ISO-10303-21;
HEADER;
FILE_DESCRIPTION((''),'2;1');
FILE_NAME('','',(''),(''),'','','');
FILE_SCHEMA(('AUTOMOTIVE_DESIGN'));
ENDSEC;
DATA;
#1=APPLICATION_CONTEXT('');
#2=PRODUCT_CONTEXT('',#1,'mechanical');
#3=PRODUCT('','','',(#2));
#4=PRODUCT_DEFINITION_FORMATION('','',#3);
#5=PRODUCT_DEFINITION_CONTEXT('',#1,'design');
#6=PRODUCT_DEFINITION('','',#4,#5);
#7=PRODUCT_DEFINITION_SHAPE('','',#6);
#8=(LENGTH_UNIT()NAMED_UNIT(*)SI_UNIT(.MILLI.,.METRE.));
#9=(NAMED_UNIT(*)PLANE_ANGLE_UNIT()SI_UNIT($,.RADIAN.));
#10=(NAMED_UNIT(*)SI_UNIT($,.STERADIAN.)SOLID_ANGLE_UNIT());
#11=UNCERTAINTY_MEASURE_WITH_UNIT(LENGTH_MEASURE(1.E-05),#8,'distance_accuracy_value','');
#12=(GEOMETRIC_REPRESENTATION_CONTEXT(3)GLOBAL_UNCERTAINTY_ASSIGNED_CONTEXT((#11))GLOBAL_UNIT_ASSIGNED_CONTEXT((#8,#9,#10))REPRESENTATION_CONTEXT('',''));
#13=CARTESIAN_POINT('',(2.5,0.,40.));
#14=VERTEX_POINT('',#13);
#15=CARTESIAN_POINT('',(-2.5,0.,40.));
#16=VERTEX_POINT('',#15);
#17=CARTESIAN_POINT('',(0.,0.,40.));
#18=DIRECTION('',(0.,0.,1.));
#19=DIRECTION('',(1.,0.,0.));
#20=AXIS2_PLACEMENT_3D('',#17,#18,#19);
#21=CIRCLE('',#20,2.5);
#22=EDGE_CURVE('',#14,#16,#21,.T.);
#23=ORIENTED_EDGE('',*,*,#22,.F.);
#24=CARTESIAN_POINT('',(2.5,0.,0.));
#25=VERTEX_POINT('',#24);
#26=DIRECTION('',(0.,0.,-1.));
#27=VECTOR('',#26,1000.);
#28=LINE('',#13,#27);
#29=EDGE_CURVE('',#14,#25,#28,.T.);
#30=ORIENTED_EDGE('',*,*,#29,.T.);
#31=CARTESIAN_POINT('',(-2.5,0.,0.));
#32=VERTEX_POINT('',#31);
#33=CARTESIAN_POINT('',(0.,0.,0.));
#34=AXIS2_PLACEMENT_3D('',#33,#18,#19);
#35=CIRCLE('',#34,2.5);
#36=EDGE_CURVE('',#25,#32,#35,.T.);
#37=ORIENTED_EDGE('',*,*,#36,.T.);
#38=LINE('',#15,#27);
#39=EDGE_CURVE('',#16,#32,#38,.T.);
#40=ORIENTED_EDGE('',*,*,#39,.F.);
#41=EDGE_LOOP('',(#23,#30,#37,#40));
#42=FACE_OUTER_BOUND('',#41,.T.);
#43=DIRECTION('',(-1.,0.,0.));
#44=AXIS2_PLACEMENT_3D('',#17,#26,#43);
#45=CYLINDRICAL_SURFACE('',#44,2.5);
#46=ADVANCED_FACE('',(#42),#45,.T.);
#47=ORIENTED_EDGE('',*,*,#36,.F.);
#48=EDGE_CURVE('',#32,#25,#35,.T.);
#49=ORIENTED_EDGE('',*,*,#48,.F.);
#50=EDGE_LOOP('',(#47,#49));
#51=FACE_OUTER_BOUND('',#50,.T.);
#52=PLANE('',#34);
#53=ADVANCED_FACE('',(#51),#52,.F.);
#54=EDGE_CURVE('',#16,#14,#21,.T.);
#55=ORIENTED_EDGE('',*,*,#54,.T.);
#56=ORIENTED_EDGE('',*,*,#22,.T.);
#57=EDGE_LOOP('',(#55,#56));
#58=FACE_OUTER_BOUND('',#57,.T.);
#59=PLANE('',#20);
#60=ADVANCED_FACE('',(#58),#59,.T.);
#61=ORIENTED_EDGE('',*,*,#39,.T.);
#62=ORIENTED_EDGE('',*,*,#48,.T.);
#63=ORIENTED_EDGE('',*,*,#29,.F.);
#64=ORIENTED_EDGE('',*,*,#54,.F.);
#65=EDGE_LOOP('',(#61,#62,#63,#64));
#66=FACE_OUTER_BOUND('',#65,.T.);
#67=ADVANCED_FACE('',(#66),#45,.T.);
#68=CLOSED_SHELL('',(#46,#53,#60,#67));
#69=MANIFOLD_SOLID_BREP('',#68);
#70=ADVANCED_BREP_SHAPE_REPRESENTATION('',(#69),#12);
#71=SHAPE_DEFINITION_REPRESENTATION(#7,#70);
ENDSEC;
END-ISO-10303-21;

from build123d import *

# Parameters (mm, degrees)
SKETCH1_R           = 2.5
BOSS_EXTRUDE1_DEPTH = 40


with BuildPart() as part:
    # Sketch1 → Boss-Extrude1 (new body)
    with BuildSketch(Plane.XY):
        Circle(SKETCH1_R)
    extrude(amount=BOSS_EXTRUDE1_DEPTH)


solid = part.part
